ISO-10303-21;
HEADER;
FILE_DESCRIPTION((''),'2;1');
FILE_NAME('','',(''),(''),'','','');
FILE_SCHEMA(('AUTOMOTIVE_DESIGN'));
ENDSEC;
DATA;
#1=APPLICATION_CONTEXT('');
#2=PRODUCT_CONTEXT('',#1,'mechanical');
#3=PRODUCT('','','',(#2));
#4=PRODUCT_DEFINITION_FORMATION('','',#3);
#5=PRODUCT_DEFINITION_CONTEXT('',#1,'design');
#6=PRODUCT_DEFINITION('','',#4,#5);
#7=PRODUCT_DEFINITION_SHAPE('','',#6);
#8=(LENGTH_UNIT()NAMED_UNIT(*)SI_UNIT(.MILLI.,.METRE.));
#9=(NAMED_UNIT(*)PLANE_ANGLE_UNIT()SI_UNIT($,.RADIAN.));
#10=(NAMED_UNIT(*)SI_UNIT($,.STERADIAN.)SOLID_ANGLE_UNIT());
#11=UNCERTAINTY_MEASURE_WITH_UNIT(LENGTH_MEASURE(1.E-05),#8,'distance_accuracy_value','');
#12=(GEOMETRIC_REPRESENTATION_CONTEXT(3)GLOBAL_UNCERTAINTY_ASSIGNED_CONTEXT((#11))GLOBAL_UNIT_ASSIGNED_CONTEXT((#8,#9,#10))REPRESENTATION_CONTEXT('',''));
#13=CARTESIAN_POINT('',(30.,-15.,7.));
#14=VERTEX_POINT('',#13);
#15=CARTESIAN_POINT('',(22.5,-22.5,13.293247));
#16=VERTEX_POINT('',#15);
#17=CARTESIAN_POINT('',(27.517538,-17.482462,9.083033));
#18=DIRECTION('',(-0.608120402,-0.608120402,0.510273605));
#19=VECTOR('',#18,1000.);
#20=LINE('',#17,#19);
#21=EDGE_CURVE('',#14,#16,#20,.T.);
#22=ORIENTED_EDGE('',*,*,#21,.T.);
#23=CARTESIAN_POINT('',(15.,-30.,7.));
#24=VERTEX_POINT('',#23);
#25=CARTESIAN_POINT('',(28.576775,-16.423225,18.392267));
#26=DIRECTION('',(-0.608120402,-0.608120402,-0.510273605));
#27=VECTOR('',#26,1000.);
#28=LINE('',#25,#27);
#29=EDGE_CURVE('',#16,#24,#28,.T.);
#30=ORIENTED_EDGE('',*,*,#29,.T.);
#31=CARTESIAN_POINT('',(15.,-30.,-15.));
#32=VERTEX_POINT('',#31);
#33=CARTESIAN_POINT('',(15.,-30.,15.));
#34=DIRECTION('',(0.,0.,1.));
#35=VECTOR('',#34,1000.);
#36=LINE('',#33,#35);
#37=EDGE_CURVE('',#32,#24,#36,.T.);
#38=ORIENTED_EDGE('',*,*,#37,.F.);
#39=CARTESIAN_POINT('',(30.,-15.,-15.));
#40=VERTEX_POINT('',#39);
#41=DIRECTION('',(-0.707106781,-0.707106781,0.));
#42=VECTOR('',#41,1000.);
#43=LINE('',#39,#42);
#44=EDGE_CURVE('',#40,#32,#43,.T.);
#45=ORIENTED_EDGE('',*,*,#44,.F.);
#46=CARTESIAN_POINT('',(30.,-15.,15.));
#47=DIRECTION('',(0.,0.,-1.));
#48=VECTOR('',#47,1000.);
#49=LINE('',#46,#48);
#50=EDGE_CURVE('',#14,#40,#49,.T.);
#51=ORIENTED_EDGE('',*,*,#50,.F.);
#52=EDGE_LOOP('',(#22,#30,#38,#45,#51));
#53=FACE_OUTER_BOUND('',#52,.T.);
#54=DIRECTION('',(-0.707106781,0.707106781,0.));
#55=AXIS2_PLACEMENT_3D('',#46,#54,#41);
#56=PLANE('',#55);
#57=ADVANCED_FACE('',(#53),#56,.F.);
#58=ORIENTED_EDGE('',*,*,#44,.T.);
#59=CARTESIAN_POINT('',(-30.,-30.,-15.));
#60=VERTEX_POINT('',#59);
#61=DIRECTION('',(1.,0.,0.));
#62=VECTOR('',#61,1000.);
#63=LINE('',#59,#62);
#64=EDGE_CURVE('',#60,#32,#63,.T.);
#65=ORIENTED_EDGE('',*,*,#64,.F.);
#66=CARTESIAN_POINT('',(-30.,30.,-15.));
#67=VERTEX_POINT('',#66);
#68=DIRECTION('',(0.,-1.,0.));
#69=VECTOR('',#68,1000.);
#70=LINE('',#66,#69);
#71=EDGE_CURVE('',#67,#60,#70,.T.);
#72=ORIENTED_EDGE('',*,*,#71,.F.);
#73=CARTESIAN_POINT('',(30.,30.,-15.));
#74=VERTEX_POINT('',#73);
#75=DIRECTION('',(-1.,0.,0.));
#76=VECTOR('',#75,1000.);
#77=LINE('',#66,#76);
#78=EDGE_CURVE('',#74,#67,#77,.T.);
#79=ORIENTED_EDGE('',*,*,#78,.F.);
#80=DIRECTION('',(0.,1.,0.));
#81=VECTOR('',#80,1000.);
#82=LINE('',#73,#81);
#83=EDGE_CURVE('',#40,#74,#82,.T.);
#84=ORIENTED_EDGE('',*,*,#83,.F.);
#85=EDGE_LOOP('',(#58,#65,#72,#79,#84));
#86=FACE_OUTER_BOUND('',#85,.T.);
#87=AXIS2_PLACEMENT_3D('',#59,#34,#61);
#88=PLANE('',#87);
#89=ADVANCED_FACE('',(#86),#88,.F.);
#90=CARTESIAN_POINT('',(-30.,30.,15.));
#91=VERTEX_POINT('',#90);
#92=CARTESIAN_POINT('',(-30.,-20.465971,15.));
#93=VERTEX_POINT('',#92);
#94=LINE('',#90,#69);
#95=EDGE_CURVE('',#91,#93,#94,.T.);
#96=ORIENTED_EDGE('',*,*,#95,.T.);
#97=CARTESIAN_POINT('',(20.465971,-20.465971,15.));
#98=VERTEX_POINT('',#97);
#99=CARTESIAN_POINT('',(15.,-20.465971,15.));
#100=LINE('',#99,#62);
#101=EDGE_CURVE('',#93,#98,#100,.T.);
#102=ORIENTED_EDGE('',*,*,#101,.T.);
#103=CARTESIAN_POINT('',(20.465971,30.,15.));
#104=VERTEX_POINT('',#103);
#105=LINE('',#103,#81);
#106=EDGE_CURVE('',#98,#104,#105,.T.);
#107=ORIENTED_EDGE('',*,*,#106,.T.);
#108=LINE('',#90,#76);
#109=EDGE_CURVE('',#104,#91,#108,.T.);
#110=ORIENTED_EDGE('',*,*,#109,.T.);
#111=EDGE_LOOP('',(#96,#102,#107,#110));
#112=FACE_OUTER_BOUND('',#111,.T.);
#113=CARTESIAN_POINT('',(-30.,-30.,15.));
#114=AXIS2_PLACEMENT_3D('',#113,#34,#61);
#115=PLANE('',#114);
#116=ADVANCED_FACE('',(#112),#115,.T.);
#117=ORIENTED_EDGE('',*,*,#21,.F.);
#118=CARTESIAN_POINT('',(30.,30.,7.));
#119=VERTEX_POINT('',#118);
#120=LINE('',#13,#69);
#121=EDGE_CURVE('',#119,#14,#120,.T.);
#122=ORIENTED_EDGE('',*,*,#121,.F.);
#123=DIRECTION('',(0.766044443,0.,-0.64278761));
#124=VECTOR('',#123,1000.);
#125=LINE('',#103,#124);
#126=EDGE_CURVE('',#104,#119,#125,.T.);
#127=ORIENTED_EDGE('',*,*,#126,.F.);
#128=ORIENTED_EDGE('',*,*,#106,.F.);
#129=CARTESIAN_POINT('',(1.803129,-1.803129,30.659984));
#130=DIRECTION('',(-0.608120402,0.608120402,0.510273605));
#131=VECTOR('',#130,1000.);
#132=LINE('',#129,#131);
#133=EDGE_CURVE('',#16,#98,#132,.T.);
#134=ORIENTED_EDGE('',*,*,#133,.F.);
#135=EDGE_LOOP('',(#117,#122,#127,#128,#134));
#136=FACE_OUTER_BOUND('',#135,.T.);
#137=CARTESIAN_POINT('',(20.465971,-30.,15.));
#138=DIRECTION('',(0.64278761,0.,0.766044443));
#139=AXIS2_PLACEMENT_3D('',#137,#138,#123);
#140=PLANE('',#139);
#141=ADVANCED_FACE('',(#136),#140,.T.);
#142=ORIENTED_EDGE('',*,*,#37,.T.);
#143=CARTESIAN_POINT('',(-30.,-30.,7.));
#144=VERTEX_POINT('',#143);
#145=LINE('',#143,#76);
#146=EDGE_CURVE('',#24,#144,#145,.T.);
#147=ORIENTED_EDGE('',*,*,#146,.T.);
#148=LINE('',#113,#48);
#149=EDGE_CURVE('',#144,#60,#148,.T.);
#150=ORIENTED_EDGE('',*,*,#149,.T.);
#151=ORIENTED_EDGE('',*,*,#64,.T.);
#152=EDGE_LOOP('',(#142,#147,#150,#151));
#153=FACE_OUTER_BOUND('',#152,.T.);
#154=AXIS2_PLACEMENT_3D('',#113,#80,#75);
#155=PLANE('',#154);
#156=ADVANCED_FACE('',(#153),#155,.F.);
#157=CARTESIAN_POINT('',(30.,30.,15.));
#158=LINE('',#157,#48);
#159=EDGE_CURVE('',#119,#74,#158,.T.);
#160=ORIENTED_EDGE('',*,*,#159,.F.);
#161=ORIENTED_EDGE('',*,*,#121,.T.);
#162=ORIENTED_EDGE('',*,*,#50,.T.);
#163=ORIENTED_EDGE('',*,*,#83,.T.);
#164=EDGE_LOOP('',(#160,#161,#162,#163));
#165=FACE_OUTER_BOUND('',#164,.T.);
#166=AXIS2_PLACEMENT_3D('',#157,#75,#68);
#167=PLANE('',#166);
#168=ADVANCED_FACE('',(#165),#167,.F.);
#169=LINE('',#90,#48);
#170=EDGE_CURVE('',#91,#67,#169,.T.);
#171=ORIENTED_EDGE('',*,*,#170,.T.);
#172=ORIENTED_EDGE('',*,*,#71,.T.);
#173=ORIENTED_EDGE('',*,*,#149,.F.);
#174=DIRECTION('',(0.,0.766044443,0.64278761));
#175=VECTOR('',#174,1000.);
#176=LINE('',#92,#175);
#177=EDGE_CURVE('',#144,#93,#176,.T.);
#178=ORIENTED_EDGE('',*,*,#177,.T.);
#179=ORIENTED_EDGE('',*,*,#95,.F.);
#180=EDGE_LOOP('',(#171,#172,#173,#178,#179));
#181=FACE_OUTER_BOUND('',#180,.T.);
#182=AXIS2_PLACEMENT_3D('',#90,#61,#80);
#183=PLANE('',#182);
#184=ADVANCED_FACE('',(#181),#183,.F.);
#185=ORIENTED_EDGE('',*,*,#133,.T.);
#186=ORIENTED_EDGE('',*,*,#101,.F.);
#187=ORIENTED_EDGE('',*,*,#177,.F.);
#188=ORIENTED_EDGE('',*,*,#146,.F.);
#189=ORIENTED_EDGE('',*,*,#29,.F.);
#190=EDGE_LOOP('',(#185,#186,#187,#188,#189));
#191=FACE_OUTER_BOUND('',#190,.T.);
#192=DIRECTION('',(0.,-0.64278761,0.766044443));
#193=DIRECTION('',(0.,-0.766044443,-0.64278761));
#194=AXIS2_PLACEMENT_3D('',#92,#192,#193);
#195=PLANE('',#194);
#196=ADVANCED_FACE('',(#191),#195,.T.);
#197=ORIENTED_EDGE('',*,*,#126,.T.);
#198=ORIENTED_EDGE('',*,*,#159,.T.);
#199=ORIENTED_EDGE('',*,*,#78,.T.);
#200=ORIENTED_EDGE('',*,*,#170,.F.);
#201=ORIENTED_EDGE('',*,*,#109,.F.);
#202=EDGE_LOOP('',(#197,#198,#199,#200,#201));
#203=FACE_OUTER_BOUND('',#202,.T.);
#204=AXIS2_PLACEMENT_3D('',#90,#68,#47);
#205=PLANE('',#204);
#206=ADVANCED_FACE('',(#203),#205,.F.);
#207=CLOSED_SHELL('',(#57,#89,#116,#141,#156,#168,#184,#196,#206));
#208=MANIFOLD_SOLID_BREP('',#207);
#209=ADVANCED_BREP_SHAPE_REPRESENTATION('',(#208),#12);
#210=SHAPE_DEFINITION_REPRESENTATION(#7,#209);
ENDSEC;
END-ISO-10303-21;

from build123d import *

# Parameters (mm, degrees)
SKETCH1_W           = 60
SKETCH1_H           = 60
BOSS_EXTRUDE1_DEPTH = 15
CHAMFER1_SIZE       = 15
CHAMFER2_SIZE       = 8
CHAMFER2_SIZE2      = 9.534028741
CHAMFER3_SIZE       = 8
CHAMFER3_SIZE2      = 9.534028741


with BuildPart() as part:
    # Sketch1 → Boss-Extrude1 (new, symmetric)
    with BuildSketch(Plane.XY):
        Rectangle(SKETCH1_W, SKETCH1_H)
    extrude(amount=BOSS_EXTRUDE1_DEPTH, both=True)

    # Chamfer1
    chamfer1_edges = [part.edges().sort_by_distance(p)[0] for p in [
        (30, -30, 0),
    ]]
    chamfer(chamfer1_edges, length=CHAMFER1_SIZE)

    # Chamfer2
    chamfer2_edges = [part.edges().sort_by_distance(p)[0] for p in [
        (-7.5, -30, 15),
    ]]
    chamfer2_side = [part.faces().sort_by_distance(p)[0] for p in [
        (-7.5, -30, 0),
    ]]
    chamfer(chamfer2_edges, length=CHAMFER2_SIZE, length2=CHAMFER2_SIZE2, reference=chamfer2_side[0])

    # Chamfer3
    chamfer3_edges = [part.edges().sort_by_distance(p)[0] for p in [
        (30, 7.5, 15),
    ]]
    chamfer3_side = [part.faces().sort_by_distance(p)[0] for p in [
        (30, 7.5, 0),
    ]]
    chamfer(chamfer3_edges, length=CHAMFER3_SIZE, length2=CHAMFER3_SIZE2, reference=chamfer3_side[0])


solid = part.part
